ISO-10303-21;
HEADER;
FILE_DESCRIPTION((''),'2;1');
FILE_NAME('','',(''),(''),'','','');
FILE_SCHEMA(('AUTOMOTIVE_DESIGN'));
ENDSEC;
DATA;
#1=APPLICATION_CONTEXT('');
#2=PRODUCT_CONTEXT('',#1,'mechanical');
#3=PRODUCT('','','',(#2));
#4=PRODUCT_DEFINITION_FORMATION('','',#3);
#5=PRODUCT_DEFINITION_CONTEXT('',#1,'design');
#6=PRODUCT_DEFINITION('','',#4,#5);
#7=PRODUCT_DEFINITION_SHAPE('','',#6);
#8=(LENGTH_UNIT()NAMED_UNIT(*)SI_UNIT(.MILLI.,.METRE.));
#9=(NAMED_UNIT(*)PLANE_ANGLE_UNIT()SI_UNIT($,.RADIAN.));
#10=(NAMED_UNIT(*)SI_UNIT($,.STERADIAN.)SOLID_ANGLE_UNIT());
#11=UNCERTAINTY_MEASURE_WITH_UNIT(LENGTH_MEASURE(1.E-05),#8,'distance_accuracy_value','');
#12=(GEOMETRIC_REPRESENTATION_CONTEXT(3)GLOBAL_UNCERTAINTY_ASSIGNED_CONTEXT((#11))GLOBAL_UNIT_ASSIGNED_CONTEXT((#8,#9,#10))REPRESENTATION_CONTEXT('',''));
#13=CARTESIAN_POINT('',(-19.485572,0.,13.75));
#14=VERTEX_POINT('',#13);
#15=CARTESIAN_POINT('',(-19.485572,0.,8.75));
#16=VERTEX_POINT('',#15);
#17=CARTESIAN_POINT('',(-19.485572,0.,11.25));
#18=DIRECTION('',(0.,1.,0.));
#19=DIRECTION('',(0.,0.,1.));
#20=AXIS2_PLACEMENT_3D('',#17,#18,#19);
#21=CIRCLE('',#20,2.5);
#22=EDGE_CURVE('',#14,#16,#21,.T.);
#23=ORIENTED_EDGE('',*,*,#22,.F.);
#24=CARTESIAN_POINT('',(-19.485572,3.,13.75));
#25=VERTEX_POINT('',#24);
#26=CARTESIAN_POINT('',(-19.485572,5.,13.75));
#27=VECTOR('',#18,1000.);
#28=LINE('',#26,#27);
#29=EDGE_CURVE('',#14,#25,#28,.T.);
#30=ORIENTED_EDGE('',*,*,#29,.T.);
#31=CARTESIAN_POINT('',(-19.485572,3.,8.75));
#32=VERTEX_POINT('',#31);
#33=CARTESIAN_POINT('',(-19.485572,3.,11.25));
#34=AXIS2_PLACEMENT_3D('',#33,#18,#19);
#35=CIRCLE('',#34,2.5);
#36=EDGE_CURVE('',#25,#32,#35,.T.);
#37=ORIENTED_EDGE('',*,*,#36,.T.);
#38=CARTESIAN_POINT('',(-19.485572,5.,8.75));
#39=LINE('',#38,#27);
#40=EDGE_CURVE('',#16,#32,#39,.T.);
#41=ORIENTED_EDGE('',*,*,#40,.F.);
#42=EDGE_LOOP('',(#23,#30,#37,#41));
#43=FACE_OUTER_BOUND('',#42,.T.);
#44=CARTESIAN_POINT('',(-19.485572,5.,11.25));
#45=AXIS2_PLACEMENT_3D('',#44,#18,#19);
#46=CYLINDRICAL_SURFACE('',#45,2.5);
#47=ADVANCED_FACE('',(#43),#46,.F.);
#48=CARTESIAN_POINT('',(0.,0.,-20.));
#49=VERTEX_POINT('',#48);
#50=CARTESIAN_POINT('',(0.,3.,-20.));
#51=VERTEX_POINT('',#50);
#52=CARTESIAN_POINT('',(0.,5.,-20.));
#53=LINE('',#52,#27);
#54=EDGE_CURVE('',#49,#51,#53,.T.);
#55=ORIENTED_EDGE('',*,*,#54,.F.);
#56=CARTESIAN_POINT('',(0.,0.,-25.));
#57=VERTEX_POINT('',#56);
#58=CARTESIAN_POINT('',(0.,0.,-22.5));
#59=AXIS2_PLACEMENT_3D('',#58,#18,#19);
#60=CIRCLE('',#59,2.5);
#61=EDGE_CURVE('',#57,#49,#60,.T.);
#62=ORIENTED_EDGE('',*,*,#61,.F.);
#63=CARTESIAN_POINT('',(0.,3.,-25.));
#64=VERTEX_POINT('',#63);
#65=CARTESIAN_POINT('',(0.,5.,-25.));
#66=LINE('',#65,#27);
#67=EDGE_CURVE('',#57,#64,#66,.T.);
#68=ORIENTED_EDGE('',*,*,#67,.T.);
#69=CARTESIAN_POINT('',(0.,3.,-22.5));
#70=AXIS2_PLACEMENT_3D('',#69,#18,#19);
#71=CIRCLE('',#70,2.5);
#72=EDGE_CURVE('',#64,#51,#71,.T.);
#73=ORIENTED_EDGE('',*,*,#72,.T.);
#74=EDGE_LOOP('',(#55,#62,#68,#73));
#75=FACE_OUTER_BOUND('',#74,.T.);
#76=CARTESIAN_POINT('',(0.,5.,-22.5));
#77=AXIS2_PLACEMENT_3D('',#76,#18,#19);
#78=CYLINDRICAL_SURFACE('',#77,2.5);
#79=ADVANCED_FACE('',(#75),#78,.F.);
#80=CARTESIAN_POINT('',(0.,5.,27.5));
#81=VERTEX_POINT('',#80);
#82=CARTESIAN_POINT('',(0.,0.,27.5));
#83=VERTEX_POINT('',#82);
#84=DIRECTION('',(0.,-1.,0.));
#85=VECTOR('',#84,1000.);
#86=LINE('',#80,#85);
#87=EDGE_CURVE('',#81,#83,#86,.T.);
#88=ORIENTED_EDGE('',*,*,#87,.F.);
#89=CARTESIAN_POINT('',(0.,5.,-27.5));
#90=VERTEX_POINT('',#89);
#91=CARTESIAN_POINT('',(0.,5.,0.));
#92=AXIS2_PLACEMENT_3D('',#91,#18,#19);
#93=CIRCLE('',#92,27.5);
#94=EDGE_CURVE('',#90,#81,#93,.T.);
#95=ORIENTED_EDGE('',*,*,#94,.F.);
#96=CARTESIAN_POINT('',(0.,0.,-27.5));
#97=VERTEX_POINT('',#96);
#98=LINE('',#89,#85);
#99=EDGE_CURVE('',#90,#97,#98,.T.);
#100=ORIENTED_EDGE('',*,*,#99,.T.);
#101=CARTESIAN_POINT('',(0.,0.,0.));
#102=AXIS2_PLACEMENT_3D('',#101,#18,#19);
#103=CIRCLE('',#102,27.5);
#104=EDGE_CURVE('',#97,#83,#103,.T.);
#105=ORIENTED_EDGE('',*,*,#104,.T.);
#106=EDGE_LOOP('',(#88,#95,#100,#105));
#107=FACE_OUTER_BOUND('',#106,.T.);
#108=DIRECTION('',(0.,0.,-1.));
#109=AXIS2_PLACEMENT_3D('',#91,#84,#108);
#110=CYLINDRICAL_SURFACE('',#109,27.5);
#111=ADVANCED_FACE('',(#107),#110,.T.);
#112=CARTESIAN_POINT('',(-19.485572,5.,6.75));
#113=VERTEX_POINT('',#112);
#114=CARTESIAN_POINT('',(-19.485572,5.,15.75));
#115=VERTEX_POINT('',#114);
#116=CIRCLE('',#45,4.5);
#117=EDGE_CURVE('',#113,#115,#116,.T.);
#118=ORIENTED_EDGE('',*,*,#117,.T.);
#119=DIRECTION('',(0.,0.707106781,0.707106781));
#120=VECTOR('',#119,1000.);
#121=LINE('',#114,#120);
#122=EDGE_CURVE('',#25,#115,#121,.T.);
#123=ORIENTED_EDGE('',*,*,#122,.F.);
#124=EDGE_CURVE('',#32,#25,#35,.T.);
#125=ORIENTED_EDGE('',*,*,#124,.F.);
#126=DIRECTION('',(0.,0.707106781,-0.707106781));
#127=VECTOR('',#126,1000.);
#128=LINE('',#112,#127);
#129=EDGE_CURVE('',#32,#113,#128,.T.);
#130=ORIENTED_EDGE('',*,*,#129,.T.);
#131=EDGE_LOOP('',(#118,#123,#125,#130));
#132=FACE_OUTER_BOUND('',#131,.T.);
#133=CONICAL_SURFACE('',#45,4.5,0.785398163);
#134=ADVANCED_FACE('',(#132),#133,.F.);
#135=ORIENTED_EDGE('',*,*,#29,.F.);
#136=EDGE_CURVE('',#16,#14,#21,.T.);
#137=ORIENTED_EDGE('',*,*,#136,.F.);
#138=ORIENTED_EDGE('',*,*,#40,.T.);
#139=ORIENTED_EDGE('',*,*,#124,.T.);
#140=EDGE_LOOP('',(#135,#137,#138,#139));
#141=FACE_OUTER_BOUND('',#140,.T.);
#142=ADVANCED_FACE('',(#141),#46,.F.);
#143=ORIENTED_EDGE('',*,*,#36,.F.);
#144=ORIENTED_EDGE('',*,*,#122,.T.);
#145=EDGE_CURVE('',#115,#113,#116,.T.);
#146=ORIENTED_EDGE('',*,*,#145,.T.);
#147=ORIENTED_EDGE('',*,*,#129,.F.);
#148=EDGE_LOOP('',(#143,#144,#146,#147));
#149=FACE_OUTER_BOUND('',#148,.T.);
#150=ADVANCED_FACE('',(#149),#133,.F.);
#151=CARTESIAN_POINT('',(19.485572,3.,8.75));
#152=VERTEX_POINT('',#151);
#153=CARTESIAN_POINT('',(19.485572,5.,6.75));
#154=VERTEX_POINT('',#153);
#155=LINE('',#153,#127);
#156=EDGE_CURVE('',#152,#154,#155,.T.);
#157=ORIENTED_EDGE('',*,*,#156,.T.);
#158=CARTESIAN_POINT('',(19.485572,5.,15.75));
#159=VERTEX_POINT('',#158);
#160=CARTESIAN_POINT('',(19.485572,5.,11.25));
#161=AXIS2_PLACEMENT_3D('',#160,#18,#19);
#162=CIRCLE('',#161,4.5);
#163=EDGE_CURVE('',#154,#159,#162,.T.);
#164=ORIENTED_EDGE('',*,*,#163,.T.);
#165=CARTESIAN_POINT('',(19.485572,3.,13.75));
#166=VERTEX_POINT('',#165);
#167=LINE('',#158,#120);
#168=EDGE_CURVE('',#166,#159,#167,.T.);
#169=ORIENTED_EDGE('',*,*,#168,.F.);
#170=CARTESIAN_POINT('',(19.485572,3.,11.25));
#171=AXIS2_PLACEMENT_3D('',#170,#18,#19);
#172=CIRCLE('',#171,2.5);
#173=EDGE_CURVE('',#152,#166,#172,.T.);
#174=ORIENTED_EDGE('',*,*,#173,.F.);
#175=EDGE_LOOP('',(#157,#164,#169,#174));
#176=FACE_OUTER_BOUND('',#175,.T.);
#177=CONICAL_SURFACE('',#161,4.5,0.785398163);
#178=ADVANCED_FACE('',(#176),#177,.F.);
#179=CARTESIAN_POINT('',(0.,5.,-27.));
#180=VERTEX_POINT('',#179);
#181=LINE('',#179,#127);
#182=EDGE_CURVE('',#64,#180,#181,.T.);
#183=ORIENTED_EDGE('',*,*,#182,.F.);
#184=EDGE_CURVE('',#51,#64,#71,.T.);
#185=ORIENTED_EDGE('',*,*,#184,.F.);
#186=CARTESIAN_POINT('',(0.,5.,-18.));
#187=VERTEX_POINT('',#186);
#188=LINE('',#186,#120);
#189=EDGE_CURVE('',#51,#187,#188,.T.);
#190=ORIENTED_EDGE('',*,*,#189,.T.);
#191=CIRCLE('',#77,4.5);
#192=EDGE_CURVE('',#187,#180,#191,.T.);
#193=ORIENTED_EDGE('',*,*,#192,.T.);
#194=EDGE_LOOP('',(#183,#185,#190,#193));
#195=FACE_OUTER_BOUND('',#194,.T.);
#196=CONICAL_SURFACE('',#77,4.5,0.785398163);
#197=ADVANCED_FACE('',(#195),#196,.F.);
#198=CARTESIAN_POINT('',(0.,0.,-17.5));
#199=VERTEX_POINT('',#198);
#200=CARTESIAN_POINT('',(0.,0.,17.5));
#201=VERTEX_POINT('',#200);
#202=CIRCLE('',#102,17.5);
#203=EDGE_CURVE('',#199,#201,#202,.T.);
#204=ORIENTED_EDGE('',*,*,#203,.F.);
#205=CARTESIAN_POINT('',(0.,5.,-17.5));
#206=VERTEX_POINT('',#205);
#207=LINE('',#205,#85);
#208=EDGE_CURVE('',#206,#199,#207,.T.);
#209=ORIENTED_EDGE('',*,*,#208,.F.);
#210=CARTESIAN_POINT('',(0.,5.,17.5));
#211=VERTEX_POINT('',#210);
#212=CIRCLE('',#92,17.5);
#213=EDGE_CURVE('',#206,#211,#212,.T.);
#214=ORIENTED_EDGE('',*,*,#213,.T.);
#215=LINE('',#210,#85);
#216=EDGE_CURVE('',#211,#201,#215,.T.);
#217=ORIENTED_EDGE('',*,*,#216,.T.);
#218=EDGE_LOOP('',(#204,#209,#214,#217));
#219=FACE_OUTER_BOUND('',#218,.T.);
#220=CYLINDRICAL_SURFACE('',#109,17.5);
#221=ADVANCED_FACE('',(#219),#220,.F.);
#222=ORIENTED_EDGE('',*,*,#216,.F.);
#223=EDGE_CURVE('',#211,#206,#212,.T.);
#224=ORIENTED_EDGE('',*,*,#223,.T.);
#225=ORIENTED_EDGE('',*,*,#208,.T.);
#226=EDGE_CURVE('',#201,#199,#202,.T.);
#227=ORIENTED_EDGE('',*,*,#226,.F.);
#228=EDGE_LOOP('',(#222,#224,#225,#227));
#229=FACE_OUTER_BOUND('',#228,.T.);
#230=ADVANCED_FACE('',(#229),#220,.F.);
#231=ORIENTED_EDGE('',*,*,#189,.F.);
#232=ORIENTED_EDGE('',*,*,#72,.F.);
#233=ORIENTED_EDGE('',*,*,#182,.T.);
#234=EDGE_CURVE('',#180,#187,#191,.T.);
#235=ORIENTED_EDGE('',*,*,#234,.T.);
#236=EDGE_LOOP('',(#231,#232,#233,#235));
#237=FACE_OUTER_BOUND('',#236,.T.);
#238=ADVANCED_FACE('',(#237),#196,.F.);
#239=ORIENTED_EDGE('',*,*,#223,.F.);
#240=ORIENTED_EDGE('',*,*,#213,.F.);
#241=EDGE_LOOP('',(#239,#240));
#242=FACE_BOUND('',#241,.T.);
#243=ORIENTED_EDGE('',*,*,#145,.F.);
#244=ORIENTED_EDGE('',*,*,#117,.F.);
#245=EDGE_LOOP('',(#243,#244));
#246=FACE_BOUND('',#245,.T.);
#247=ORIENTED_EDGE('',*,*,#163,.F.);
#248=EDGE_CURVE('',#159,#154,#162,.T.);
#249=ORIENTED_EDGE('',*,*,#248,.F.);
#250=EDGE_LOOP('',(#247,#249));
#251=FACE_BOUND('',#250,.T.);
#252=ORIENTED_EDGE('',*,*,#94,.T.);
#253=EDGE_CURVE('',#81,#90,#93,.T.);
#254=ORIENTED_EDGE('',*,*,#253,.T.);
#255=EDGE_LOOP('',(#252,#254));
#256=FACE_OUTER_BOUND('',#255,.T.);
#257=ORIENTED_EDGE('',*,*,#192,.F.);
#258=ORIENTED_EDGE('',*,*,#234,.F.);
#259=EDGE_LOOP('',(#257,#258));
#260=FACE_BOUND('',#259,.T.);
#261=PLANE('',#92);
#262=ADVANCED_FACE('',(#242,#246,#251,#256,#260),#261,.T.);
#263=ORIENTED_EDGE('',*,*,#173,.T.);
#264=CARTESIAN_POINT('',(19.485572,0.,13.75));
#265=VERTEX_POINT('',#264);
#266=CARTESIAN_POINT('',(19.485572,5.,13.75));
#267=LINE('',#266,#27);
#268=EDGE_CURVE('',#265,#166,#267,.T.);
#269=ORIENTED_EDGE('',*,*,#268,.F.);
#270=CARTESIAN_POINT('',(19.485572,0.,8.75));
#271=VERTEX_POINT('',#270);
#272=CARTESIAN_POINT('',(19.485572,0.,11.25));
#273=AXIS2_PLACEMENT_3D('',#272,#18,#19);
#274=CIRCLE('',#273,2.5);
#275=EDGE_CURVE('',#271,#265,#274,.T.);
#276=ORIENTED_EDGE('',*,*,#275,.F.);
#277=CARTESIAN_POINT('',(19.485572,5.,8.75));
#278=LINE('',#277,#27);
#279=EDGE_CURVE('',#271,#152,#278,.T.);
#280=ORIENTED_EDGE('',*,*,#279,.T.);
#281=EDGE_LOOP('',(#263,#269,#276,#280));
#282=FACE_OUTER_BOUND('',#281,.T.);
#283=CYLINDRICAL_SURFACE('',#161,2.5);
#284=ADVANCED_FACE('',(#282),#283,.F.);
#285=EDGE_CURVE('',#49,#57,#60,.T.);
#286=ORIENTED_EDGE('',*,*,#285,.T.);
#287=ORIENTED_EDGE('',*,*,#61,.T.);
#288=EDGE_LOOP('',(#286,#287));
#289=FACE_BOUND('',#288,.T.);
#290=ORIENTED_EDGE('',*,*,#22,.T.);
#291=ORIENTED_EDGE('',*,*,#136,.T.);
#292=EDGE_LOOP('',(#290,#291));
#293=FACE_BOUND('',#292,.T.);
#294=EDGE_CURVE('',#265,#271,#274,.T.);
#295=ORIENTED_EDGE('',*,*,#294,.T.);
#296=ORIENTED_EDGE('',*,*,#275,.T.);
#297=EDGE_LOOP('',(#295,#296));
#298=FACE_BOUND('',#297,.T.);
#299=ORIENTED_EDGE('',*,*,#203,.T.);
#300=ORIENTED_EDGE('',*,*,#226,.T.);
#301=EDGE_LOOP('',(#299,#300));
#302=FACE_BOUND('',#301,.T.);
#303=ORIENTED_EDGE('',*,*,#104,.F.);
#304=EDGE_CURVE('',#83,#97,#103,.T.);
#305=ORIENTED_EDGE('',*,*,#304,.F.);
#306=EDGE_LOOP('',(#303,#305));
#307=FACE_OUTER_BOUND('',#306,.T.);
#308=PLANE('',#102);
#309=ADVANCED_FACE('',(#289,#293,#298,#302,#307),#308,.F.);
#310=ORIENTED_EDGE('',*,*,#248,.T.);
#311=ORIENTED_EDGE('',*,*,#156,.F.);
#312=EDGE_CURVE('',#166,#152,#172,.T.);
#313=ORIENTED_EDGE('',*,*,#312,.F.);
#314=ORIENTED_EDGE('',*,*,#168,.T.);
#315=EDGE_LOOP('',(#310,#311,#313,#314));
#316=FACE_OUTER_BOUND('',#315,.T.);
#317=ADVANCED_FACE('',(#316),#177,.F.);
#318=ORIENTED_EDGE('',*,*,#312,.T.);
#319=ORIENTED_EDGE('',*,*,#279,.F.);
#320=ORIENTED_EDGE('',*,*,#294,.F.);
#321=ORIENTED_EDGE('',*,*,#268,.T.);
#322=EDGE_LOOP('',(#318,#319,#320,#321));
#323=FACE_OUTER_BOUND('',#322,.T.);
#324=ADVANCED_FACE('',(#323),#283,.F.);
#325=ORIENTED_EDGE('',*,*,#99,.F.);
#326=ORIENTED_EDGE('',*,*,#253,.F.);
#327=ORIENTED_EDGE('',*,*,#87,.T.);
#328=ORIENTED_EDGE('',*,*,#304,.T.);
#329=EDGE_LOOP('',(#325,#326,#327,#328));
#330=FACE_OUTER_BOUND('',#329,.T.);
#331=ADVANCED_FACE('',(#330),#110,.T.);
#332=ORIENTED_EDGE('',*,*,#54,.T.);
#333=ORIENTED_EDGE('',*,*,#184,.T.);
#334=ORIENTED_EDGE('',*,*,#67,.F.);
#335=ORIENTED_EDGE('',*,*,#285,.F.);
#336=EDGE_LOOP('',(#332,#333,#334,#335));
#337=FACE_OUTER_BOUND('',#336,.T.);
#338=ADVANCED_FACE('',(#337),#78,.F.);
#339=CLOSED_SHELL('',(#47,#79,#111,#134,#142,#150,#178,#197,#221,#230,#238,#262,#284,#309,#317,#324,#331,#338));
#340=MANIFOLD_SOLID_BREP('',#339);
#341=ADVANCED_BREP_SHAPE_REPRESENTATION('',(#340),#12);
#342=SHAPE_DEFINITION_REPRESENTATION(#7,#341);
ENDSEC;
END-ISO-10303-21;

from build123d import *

# Parameters (mm, degrees)
SKETCH1_R           = 27.5
SKETCH1_R_2         = 17.5
BOSS_EXTRUDE1_DEPTH = 5
HOLE1_D             = 5
HOLE1_CSINK_D       = 9
HOLE1_CSINK_ANGLE   = 90


with BuildPart() as part:
    # Sketch1 → Boss-Extrude1 (new body)
    with BuildSketch(Plane(origin=(0, 0, 0), x_dir=(1, 0, 0), z_dir=(0, 1, 0))):
        with Locations(Location((0, 0, 0), (0, 0, 270))):
            Circle(SKETCH1_R)
        with Locations(Location((0, 0, 0), (0, 0, 270))):
            Circle(SKETCH1_R_2, mode=Mode.SUBTRACT)
    extrude(amount=BOSS_EXTRUDE1_DEPTH)

    # Hole1 (through all)
    with Locations(Plane(origin=(0, 5, 0), x_dir=(1, 0, 0), z_dir=(0, 1, 0))):
        with Locations((-19.485571585, -11.25), (0, 22.5), (19.485571585, -11.25)):
            CounterSinkHole(HOLE1_D / 2, HOLE1_CSINK_D / 2, counter_sink_angle=HOLE1_CSINK_ANGLE)


solid = part.part
